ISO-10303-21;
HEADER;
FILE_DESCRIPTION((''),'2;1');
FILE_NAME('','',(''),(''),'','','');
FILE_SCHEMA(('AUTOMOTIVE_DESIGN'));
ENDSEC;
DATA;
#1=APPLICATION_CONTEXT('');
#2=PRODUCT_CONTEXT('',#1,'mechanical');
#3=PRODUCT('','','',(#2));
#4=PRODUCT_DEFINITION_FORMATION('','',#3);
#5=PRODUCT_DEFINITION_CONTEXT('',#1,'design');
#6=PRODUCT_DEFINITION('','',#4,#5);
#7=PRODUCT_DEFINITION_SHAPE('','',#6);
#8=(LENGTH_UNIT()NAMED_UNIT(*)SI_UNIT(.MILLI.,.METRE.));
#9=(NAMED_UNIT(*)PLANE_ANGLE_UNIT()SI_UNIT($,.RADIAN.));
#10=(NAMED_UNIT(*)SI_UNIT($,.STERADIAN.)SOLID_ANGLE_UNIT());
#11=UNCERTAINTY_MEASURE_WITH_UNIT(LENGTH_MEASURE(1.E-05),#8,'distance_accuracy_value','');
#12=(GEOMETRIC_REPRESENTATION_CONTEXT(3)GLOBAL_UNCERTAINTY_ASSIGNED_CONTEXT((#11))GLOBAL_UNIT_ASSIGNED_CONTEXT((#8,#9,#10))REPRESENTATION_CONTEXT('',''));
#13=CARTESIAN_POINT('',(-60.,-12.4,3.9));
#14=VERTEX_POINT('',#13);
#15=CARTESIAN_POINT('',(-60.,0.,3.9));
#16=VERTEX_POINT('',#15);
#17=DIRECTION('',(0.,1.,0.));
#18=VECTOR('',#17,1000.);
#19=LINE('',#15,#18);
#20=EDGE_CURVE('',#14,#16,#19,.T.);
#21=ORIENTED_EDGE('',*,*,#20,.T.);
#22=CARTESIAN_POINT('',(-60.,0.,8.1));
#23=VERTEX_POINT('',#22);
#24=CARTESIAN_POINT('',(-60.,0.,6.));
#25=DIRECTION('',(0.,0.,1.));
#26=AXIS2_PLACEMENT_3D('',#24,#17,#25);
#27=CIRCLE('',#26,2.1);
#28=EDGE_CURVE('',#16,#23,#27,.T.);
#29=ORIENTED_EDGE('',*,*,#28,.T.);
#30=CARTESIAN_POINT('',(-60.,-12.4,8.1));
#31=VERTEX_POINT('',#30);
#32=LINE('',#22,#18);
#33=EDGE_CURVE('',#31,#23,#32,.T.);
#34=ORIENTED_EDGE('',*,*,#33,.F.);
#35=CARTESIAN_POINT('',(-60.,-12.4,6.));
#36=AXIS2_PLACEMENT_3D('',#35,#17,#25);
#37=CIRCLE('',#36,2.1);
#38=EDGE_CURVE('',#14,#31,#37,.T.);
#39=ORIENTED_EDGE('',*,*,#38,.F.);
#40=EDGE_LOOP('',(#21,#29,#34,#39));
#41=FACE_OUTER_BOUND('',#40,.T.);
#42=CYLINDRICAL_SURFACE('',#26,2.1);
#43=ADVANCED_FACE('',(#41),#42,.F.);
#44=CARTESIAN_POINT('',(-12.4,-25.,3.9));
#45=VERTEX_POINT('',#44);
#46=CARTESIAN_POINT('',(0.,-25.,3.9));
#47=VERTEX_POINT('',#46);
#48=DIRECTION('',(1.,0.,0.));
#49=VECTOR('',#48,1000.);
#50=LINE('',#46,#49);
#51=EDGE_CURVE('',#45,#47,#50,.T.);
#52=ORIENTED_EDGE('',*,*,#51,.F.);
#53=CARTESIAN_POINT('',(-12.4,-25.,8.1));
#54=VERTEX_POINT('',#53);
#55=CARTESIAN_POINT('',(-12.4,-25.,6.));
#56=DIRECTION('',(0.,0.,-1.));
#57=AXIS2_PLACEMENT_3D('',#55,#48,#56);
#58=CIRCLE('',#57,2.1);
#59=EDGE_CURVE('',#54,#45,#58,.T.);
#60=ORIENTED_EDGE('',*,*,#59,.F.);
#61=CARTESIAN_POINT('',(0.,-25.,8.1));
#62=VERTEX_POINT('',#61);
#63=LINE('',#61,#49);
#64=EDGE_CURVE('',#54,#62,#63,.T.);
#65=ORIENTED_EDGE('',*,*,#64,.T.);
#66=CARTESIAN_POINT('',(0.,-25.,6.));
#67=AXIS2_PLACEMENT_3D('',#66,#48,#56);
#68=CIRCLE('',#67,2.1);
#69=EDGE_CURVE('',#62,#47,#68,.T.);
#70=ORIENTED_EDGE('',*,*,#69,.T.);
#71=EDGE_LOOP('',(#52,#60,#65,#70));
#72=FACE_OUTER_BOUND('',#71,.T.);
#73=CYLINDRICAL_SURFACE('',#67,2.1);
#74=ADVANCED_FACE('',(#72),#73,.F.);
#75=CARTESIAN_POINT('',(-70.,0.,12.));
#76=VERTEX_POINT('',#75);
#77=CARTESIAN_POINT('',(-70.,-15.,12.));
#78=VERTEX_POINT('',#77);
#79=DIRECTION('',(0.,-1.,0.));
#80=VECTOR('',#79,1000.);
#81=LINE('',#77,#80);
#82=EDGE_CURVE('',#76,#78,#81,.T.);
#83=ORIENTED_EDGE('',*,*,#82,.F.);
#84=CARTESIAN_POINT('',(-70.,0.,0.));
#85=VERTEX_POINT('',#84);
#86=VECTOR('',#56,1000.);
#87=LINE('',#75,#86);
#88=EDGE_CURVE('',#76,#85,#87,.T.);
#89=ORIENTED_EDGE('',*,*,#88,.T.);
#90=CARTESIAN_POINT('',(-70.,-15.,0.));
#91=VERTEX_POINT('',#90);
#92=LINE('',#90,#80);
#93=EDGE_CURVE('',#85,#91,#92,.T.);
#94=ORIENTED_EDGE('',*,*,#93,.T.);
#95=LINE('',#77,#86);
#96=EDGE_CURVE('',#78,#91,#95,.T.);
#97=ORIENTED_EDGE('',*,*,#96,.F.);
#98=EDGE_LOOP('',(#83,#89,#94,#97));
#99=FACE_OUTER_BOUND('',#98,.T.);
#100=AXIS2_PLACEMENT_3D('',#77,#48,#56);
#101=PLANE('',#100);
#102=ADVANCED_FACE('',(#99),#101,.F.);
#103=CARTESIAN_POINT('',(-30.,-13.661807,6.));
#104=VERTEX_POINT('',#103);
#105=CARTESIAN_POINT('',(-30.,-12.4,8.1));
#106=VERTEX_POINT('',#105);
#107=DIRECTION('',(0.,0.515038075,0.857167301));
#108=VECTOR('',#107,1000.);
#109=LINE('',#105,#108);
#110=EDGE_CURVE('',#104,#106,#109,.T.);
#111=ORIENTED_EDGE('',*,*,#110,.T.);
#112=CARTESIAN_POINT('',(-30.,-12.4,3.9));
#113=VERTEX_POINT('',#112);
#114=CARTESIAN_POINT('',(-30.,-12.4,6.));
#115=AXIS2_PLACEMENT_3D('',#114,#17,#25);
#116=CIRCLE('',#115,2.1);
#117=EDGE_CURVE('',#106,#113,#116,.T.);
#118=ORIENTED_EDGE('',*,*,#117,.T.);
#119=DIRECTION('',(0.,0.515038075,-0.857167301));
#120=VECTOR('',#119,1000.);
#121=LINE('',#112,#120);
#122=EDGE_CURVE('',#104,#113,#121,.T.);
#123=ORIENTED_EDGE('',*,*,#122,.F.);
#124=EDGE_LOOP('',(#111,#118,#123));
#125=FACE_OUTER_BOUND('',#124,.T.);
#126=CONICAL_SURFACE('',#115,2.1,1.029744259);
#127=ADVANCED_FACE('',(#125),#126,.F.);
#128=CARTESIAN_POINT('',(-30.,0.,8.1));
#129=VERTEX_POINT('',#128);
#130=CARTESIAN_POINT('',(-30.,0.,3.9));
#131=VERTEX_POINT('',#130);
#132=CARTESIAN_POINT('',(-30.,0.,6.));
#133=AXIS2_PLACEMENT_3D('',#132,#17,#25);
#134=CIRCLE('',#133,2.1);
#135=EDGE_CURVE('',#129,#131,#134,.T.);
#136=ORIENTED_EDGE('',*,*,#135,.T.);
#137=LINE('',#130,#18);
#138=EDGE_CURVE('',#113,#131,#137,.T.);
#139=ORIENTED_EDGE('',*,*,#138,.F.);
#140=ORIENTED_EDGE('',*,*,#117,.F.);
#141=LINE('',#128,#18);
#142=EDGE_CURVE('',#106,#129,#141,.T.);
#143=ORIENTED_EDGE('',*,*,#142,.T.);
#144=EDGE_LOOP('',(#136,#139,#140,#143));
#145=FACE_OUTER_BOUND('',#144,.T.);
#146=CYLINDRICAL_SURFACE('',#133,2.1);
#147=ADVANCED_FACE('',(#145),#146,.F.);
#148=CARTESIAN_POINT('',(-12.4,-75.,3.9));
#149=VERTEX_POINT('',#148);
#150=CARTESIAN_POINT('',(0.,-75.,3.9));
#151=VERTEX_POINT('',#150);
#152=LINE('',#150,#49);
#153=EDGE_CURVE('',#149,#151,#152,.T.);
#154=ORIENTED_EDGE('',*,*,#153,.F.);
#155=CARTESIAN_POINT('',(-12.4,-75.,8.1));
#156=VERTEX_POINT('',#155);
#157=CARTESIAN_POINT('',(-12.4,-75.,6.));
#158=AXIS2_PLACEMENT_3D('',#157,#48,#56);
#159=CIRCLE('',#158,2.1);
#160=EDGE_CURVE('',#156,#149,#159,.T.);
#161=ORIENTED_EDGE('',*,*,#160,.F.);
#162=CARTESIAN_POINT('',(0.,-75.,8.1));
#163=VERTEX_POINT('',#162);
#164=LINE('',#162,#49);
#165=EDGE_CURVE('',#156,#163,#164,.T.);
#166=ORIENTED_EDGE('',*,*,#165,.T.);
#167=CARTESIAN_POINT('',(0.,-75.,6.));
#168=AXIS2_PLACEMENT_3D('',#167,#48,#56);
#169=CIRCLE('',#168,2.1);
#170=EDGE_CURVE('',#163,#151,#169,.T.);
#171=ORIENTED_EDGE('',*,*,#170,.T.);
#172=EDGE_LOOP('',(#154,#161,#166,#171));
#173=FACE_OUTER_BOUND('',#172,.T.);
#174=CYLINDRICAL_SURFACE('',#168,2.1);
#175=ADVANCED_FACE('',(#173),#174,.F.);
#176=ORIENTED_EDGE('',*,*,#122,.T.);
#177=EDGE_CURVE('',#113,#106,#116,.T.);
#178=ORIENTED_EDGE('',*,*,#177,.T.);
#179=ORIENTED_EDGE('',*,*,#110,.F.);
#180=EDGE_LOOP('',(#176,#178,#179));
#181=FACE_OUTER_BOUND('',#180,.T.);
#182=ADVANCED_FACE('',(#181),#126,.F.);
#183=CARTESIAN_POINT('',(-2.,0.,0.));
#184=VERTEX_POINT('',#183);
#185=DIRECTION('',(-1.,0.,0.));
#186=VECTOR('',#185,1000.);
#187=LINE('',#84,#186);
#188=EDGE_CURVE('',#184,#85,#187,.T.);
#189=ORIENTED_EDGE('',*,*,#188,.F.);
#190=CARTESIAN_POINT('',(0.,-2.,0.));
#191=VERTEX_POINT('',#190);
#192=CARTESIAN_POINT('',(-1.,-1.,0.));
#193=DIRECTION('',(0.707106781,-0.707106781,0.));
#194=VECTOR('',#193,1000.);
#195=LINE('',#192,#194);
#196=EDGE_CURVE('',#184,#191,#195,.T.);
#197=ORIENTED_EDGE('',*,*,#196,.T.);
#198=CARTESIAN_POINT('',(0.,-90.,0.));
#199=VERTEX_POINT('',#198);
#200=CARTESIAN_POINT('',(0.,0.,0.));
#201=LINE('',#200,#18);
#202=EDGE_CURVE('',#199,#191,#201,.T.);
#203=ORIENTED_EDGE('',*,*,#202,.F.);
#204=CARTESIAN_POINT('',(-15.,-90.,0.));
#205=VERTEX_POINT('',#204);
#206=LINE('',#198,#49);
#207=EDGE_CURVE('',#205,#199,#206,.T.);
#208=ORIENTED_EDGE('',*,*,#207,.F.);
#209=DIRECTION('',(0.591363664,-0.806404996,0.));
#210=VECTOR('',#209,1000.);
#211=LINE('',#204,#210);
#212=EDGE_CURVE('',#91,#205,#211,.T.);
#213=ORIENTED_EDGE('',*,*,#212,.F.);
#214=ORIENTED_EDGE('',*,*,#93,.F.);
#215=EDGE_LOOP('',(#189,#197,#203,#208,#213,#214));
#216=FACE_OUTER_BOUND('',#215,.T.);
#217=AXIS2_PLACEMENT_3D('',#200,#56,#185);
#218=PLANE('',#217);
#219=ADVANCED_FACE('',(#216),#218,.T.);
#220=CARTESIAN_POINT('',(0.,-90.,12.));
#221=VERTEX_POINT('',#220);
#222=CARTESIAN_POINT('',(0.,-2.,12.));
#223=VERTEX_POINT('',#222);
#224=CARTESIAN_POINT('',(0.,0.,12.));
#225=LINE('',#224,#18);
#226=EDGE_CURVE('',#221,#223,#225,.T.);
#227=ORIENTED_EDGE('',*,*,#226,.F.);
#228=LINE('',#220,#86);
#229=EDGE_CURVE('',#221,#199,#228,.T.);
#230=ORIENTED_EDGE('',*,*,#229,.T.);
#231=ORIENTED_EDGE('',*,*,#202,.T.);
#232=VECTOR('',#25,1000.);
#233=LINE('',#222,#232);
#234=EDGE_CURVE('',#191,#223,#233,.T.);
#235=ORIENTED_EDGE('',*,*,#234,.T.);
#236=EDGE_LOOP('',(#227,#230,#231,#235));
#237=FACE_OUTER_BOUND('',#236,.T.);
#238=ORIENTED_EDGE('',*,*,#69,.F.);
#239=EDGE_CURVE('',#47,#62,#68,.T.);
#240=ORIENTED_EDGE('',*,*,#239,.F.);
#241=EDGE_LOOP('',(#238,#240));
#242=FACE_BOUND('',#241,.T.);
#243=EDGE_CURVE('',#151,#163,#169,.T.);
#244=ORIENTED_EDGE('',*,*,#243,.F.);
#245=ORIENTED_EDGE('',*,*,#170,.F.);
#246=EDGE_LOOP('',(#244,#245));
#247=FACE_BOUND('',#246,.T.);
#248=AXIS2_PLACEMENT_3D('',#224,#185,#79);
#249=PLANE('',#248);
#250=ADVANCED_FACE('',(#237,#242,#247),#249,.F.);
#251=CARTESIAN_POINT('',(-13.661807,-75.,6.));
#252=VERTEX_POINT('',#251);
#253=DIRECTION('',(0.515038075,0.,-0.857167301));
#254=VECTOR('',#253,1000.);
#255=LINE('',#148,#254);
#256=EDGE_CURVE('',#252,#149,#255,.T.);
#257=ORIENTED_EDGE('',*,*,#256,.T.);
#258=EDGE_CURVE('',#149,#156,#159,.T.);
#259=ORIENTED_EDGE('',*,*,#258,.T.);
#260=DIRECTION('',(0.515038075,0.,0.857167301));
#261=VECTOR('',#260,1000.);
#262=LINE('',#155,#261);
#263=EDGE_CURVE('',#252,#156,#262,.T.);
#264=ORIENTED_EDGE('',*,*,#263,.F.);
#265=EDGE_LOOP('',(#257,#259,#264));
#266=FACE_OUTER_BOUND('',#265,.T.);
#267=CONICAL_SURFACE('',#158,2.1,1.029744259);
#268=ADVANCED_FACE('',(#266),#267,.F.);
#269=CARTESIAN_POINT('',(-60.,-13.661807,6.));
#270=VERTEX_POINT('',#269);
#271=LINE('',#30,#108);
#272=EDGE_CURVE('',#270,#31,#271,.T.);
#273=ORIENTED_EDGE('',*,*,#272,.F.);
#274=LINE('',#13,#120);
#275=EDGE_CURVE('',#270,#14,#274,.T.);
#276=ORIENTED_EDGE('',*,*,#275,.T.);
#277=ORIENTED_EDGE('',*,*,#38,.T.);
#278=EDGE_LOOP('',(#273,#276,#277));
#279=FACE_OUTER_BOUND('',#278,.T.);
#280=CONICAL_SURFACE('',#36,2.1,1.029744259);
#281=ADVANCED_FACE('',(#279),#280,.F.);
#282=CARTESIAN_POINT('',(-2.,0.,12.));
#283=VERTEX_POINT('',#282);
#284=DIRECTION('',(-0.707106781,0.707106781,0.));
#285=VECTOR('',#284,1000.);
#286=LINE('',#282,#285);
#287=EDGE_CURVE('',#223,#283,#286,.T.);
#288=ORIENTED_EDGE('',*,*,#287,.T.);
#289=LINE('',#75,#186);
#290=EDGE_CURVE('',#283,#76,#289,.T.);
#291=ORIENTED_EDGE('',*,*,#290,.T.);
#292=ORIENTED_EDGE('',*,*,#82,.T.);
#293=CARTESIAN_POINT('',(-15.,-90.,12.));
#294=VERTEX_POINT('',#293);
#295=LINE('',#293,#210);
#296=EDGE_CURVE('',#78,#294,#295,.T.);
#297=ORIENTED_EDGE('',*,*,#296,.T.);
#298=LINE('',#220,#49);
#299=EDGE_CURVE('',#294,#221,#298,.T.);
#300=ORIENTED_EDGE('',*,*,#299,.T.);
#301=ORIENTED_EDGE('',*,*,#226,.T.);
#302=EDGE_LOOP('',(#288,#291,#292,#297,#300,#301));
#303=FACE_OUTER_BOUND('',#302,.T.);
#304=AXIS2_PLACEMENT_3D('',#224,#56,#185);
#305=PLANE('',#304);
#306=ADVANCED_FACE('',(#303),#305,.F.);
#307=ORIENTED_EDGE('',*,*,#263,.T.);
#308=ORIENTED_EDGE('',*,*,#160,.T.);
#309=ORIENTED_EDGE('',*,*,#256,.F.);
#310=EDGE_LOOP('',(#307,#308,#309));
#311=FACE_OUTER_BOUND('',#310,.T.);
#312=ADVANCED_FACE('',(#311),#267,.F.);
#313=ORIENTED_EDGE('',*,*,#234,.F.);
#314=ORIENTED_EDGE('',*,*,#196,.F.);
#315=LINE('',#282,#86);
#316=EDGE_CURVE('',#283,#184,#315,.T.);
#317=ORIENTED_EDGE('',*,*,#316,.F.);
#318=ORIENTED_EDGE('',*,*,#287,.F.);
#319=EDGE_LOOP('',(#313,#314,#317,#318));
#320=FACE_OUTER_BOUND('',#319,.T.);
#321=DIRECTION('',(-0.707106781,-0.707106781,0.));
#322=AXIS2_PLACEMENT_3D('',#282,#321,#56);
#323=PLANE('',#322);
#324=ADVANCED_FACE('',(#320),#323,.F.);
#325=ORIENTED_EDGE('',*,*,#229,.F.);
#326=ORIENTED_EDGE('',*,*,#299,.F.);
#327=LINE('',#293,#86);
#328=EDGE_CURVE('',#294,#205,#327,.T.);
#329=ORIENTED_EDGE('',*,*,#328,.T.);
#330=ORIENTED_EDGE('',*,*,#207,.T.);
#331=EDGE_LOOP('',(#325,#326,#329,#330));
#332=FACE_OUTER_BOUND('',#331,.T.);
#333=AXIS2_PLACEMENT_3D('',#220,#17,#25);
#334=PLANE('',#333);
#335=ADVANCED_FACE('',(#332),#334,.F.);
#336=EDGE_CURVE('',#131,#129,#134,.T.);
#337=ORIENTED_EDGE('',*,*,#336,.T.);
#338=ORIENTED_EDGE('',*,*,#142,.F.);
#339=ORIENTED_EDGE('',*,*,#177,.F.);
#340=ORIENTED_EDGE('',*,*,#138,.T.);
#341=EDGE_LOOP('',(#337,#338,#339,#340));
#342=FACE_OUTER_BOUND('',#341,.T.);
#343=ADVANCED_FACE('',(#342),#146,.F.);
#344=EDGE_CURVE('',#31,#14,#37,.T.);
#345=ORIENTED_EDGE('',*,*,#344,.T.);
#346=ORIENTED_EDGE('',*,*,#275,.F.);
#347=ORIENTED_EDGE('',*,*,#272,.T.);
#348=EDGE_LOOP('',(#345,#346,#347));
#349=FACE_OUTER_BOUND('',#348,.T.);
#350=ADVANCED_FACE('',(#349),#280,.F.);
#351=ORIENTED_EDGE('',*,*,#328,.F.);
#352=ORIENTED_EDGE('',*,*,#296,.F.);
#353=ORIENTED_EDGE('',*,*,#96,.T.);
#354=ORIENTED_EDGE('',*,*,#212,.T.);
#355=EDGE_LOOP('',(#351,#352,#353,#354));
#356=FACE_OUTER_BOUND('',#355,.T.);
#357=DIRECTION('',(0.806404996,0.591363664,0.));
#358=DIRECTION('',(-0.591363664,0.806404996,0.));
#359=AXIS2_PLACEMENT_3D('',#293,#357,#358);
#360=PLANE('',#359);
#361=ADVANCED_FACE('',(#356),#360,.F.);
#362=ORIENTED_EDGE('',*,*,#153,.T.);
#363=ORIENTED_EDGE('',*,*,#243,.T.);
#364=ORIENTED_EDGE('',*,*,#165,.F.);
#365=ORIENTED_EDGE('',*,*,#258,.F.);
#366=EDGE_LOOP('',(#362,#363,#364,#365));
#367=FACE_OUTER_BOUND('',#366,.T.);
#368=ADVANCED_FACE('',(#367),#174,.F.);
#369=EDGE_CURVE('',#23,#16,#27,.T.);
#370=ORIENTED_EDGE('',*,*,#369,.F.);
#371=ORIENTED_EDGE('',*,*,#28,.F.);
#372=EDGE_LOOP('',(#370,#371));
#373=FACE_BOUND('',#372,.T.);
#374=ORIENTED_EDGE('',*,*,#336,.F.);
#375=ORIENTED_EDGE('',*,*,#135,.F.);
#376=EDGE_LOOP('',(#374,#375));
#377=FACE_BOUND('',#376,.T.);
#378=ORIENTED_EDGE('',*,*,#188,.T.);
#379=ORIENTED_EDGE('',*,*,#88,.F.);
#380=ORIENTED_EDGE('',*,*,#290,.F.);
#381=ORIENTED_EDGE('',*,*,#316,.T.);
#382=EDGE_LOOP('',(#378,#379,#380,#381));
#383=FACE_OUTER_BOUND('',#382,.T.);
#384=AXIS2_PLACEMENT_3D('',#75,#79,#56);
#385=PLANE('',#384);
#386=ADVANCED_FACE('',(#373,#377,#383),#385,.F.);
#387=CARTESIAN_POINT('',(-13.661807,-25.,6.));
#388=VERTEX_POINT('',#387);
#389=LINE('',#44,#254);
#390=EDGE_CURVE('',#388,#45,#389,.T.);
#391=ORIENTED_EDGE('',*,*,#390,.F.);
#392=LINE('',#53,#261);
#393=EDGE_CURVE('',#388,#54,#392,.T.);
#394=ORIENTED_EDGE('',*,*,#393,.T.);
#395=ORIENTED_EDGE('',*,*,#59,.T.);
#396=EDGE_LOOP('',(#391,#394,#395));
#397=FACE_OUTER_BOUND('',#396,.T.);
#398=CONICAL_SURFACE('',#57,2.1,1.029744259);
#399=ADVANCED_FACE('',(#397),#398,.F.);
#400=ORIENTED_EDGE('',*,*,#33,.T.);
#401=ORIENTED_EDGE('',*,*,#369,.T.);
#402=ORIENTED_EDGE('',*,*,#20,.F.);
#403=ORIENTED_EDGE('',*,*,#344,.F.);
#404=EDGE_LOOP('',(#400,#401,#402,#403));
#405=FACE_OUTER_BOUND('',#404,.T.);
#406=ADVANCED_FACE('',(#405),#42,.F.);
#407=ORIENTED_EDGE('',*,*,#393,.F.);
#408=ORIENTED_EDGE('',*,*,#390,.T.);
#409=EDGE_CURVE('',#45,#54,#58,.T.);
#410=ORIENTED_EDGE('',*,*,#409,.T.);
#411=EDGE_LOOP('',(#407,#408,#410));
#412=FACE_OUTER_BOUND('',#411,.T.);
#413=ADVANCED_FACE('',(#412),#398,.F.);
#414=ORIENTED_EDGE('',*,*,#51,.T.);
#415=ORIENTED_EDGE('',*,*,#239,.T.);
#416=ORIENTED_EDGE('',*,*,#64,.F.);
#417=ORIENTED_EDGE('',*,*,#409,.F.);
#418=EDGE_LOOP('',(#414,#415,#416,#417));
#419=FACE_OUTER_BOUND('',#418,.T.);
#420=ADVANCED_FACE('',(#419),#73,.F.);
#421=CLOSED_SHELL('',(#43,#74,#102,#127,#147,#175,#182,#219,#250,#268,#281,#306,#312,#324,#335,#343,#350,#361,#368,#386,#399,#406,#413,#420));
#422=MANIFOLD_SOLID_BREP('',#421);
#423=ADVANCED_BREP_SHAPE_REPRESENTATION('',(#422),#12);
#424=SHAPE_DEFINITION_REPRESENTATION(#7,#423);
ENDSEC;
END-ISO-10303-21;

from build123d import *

# Parameters (mm, degrees)
EXTRUDE_1_DEPTH        = 12
HOLE_WIZARD_M5_1_D     = 4.2
HOLE_WIZARD_M5_1_DEPTH = 12.4
HOLE_WIZARD_M5_1_TIP   = 1.2618073
HOLE_WIZARD_M5_2_D     = 4.2
HOLE_WIZARD_M5_2_DEPTH = 12.4
HOLE_WIZARD_M5_2_TIP   = 1.2618073
CHAMFER_1_SIZE         = 2


with BuildPart() as part:
    # 草图1 → 凸台-拉伸1 (new body)
    with BuildSketch(Plane.XY):
        Polygon((0, 0), (0, -90), (-15, -90), (-70, -15), (-70, 0), align=None)
    extrude(amount=EXTRUDE_1_DEPTH)

    # M5 螺纹孔1
    with Locations(Plane(origin=(0, 0, 0), x_dir=(1, 0, 0), z_dir=(0, 1, 0))):
        with Locations((-60, -6), (-30, -6)):
            Hole(HOLE_WIZARD_M5_1_D / 2, depth=HOLE_WIZARD_M5_1_DEPTH)
            with Locations((0, 0, -(HOLE_WIZARD_M5_1_DEPTH + HOLE_WIZARD_M5_1_TIP / 2))):  # 118° drill point
                Cone(0, HOLE_WIZARD_M5_1_D / 2, HOLE_WIZARD_M5_1_TIP, mode=Mode.SUBTRACT)

    # M5 螺纹孔2
    with Locations(Plane(origin=(0, 0, 0), x_dir=(0, 0, -1), z_dir=(1, 0, 0))):
        with Locations((-6, -75), (-6, -25)):
            Hole(HOLE_WIZARD_M5_2_D / 2, depth=HOLE_WIZARD_M5_2_DEPTH)
            with Locations((0, 0, -(HOLE_WIZARD_M5_2_DEPTH + HOLE_WIZARD_M5_2_TIP / 2))):  # 118° drill point
                Cone(0, HOLE_WIZARD_M5_2_D / 2, HOLE_WIZARD_M5_2_TIP, mode=Mode.SUBTRACT)

    # 倒角1
    chamfer_1_edges = [part.edges().sort_by_distance(p)[0] for p in [
        (0, 0, 6),
    ]]
    chamfer(chamfer_1_edges, length=CHAMFER_1_SIZE)


solid = part.part
